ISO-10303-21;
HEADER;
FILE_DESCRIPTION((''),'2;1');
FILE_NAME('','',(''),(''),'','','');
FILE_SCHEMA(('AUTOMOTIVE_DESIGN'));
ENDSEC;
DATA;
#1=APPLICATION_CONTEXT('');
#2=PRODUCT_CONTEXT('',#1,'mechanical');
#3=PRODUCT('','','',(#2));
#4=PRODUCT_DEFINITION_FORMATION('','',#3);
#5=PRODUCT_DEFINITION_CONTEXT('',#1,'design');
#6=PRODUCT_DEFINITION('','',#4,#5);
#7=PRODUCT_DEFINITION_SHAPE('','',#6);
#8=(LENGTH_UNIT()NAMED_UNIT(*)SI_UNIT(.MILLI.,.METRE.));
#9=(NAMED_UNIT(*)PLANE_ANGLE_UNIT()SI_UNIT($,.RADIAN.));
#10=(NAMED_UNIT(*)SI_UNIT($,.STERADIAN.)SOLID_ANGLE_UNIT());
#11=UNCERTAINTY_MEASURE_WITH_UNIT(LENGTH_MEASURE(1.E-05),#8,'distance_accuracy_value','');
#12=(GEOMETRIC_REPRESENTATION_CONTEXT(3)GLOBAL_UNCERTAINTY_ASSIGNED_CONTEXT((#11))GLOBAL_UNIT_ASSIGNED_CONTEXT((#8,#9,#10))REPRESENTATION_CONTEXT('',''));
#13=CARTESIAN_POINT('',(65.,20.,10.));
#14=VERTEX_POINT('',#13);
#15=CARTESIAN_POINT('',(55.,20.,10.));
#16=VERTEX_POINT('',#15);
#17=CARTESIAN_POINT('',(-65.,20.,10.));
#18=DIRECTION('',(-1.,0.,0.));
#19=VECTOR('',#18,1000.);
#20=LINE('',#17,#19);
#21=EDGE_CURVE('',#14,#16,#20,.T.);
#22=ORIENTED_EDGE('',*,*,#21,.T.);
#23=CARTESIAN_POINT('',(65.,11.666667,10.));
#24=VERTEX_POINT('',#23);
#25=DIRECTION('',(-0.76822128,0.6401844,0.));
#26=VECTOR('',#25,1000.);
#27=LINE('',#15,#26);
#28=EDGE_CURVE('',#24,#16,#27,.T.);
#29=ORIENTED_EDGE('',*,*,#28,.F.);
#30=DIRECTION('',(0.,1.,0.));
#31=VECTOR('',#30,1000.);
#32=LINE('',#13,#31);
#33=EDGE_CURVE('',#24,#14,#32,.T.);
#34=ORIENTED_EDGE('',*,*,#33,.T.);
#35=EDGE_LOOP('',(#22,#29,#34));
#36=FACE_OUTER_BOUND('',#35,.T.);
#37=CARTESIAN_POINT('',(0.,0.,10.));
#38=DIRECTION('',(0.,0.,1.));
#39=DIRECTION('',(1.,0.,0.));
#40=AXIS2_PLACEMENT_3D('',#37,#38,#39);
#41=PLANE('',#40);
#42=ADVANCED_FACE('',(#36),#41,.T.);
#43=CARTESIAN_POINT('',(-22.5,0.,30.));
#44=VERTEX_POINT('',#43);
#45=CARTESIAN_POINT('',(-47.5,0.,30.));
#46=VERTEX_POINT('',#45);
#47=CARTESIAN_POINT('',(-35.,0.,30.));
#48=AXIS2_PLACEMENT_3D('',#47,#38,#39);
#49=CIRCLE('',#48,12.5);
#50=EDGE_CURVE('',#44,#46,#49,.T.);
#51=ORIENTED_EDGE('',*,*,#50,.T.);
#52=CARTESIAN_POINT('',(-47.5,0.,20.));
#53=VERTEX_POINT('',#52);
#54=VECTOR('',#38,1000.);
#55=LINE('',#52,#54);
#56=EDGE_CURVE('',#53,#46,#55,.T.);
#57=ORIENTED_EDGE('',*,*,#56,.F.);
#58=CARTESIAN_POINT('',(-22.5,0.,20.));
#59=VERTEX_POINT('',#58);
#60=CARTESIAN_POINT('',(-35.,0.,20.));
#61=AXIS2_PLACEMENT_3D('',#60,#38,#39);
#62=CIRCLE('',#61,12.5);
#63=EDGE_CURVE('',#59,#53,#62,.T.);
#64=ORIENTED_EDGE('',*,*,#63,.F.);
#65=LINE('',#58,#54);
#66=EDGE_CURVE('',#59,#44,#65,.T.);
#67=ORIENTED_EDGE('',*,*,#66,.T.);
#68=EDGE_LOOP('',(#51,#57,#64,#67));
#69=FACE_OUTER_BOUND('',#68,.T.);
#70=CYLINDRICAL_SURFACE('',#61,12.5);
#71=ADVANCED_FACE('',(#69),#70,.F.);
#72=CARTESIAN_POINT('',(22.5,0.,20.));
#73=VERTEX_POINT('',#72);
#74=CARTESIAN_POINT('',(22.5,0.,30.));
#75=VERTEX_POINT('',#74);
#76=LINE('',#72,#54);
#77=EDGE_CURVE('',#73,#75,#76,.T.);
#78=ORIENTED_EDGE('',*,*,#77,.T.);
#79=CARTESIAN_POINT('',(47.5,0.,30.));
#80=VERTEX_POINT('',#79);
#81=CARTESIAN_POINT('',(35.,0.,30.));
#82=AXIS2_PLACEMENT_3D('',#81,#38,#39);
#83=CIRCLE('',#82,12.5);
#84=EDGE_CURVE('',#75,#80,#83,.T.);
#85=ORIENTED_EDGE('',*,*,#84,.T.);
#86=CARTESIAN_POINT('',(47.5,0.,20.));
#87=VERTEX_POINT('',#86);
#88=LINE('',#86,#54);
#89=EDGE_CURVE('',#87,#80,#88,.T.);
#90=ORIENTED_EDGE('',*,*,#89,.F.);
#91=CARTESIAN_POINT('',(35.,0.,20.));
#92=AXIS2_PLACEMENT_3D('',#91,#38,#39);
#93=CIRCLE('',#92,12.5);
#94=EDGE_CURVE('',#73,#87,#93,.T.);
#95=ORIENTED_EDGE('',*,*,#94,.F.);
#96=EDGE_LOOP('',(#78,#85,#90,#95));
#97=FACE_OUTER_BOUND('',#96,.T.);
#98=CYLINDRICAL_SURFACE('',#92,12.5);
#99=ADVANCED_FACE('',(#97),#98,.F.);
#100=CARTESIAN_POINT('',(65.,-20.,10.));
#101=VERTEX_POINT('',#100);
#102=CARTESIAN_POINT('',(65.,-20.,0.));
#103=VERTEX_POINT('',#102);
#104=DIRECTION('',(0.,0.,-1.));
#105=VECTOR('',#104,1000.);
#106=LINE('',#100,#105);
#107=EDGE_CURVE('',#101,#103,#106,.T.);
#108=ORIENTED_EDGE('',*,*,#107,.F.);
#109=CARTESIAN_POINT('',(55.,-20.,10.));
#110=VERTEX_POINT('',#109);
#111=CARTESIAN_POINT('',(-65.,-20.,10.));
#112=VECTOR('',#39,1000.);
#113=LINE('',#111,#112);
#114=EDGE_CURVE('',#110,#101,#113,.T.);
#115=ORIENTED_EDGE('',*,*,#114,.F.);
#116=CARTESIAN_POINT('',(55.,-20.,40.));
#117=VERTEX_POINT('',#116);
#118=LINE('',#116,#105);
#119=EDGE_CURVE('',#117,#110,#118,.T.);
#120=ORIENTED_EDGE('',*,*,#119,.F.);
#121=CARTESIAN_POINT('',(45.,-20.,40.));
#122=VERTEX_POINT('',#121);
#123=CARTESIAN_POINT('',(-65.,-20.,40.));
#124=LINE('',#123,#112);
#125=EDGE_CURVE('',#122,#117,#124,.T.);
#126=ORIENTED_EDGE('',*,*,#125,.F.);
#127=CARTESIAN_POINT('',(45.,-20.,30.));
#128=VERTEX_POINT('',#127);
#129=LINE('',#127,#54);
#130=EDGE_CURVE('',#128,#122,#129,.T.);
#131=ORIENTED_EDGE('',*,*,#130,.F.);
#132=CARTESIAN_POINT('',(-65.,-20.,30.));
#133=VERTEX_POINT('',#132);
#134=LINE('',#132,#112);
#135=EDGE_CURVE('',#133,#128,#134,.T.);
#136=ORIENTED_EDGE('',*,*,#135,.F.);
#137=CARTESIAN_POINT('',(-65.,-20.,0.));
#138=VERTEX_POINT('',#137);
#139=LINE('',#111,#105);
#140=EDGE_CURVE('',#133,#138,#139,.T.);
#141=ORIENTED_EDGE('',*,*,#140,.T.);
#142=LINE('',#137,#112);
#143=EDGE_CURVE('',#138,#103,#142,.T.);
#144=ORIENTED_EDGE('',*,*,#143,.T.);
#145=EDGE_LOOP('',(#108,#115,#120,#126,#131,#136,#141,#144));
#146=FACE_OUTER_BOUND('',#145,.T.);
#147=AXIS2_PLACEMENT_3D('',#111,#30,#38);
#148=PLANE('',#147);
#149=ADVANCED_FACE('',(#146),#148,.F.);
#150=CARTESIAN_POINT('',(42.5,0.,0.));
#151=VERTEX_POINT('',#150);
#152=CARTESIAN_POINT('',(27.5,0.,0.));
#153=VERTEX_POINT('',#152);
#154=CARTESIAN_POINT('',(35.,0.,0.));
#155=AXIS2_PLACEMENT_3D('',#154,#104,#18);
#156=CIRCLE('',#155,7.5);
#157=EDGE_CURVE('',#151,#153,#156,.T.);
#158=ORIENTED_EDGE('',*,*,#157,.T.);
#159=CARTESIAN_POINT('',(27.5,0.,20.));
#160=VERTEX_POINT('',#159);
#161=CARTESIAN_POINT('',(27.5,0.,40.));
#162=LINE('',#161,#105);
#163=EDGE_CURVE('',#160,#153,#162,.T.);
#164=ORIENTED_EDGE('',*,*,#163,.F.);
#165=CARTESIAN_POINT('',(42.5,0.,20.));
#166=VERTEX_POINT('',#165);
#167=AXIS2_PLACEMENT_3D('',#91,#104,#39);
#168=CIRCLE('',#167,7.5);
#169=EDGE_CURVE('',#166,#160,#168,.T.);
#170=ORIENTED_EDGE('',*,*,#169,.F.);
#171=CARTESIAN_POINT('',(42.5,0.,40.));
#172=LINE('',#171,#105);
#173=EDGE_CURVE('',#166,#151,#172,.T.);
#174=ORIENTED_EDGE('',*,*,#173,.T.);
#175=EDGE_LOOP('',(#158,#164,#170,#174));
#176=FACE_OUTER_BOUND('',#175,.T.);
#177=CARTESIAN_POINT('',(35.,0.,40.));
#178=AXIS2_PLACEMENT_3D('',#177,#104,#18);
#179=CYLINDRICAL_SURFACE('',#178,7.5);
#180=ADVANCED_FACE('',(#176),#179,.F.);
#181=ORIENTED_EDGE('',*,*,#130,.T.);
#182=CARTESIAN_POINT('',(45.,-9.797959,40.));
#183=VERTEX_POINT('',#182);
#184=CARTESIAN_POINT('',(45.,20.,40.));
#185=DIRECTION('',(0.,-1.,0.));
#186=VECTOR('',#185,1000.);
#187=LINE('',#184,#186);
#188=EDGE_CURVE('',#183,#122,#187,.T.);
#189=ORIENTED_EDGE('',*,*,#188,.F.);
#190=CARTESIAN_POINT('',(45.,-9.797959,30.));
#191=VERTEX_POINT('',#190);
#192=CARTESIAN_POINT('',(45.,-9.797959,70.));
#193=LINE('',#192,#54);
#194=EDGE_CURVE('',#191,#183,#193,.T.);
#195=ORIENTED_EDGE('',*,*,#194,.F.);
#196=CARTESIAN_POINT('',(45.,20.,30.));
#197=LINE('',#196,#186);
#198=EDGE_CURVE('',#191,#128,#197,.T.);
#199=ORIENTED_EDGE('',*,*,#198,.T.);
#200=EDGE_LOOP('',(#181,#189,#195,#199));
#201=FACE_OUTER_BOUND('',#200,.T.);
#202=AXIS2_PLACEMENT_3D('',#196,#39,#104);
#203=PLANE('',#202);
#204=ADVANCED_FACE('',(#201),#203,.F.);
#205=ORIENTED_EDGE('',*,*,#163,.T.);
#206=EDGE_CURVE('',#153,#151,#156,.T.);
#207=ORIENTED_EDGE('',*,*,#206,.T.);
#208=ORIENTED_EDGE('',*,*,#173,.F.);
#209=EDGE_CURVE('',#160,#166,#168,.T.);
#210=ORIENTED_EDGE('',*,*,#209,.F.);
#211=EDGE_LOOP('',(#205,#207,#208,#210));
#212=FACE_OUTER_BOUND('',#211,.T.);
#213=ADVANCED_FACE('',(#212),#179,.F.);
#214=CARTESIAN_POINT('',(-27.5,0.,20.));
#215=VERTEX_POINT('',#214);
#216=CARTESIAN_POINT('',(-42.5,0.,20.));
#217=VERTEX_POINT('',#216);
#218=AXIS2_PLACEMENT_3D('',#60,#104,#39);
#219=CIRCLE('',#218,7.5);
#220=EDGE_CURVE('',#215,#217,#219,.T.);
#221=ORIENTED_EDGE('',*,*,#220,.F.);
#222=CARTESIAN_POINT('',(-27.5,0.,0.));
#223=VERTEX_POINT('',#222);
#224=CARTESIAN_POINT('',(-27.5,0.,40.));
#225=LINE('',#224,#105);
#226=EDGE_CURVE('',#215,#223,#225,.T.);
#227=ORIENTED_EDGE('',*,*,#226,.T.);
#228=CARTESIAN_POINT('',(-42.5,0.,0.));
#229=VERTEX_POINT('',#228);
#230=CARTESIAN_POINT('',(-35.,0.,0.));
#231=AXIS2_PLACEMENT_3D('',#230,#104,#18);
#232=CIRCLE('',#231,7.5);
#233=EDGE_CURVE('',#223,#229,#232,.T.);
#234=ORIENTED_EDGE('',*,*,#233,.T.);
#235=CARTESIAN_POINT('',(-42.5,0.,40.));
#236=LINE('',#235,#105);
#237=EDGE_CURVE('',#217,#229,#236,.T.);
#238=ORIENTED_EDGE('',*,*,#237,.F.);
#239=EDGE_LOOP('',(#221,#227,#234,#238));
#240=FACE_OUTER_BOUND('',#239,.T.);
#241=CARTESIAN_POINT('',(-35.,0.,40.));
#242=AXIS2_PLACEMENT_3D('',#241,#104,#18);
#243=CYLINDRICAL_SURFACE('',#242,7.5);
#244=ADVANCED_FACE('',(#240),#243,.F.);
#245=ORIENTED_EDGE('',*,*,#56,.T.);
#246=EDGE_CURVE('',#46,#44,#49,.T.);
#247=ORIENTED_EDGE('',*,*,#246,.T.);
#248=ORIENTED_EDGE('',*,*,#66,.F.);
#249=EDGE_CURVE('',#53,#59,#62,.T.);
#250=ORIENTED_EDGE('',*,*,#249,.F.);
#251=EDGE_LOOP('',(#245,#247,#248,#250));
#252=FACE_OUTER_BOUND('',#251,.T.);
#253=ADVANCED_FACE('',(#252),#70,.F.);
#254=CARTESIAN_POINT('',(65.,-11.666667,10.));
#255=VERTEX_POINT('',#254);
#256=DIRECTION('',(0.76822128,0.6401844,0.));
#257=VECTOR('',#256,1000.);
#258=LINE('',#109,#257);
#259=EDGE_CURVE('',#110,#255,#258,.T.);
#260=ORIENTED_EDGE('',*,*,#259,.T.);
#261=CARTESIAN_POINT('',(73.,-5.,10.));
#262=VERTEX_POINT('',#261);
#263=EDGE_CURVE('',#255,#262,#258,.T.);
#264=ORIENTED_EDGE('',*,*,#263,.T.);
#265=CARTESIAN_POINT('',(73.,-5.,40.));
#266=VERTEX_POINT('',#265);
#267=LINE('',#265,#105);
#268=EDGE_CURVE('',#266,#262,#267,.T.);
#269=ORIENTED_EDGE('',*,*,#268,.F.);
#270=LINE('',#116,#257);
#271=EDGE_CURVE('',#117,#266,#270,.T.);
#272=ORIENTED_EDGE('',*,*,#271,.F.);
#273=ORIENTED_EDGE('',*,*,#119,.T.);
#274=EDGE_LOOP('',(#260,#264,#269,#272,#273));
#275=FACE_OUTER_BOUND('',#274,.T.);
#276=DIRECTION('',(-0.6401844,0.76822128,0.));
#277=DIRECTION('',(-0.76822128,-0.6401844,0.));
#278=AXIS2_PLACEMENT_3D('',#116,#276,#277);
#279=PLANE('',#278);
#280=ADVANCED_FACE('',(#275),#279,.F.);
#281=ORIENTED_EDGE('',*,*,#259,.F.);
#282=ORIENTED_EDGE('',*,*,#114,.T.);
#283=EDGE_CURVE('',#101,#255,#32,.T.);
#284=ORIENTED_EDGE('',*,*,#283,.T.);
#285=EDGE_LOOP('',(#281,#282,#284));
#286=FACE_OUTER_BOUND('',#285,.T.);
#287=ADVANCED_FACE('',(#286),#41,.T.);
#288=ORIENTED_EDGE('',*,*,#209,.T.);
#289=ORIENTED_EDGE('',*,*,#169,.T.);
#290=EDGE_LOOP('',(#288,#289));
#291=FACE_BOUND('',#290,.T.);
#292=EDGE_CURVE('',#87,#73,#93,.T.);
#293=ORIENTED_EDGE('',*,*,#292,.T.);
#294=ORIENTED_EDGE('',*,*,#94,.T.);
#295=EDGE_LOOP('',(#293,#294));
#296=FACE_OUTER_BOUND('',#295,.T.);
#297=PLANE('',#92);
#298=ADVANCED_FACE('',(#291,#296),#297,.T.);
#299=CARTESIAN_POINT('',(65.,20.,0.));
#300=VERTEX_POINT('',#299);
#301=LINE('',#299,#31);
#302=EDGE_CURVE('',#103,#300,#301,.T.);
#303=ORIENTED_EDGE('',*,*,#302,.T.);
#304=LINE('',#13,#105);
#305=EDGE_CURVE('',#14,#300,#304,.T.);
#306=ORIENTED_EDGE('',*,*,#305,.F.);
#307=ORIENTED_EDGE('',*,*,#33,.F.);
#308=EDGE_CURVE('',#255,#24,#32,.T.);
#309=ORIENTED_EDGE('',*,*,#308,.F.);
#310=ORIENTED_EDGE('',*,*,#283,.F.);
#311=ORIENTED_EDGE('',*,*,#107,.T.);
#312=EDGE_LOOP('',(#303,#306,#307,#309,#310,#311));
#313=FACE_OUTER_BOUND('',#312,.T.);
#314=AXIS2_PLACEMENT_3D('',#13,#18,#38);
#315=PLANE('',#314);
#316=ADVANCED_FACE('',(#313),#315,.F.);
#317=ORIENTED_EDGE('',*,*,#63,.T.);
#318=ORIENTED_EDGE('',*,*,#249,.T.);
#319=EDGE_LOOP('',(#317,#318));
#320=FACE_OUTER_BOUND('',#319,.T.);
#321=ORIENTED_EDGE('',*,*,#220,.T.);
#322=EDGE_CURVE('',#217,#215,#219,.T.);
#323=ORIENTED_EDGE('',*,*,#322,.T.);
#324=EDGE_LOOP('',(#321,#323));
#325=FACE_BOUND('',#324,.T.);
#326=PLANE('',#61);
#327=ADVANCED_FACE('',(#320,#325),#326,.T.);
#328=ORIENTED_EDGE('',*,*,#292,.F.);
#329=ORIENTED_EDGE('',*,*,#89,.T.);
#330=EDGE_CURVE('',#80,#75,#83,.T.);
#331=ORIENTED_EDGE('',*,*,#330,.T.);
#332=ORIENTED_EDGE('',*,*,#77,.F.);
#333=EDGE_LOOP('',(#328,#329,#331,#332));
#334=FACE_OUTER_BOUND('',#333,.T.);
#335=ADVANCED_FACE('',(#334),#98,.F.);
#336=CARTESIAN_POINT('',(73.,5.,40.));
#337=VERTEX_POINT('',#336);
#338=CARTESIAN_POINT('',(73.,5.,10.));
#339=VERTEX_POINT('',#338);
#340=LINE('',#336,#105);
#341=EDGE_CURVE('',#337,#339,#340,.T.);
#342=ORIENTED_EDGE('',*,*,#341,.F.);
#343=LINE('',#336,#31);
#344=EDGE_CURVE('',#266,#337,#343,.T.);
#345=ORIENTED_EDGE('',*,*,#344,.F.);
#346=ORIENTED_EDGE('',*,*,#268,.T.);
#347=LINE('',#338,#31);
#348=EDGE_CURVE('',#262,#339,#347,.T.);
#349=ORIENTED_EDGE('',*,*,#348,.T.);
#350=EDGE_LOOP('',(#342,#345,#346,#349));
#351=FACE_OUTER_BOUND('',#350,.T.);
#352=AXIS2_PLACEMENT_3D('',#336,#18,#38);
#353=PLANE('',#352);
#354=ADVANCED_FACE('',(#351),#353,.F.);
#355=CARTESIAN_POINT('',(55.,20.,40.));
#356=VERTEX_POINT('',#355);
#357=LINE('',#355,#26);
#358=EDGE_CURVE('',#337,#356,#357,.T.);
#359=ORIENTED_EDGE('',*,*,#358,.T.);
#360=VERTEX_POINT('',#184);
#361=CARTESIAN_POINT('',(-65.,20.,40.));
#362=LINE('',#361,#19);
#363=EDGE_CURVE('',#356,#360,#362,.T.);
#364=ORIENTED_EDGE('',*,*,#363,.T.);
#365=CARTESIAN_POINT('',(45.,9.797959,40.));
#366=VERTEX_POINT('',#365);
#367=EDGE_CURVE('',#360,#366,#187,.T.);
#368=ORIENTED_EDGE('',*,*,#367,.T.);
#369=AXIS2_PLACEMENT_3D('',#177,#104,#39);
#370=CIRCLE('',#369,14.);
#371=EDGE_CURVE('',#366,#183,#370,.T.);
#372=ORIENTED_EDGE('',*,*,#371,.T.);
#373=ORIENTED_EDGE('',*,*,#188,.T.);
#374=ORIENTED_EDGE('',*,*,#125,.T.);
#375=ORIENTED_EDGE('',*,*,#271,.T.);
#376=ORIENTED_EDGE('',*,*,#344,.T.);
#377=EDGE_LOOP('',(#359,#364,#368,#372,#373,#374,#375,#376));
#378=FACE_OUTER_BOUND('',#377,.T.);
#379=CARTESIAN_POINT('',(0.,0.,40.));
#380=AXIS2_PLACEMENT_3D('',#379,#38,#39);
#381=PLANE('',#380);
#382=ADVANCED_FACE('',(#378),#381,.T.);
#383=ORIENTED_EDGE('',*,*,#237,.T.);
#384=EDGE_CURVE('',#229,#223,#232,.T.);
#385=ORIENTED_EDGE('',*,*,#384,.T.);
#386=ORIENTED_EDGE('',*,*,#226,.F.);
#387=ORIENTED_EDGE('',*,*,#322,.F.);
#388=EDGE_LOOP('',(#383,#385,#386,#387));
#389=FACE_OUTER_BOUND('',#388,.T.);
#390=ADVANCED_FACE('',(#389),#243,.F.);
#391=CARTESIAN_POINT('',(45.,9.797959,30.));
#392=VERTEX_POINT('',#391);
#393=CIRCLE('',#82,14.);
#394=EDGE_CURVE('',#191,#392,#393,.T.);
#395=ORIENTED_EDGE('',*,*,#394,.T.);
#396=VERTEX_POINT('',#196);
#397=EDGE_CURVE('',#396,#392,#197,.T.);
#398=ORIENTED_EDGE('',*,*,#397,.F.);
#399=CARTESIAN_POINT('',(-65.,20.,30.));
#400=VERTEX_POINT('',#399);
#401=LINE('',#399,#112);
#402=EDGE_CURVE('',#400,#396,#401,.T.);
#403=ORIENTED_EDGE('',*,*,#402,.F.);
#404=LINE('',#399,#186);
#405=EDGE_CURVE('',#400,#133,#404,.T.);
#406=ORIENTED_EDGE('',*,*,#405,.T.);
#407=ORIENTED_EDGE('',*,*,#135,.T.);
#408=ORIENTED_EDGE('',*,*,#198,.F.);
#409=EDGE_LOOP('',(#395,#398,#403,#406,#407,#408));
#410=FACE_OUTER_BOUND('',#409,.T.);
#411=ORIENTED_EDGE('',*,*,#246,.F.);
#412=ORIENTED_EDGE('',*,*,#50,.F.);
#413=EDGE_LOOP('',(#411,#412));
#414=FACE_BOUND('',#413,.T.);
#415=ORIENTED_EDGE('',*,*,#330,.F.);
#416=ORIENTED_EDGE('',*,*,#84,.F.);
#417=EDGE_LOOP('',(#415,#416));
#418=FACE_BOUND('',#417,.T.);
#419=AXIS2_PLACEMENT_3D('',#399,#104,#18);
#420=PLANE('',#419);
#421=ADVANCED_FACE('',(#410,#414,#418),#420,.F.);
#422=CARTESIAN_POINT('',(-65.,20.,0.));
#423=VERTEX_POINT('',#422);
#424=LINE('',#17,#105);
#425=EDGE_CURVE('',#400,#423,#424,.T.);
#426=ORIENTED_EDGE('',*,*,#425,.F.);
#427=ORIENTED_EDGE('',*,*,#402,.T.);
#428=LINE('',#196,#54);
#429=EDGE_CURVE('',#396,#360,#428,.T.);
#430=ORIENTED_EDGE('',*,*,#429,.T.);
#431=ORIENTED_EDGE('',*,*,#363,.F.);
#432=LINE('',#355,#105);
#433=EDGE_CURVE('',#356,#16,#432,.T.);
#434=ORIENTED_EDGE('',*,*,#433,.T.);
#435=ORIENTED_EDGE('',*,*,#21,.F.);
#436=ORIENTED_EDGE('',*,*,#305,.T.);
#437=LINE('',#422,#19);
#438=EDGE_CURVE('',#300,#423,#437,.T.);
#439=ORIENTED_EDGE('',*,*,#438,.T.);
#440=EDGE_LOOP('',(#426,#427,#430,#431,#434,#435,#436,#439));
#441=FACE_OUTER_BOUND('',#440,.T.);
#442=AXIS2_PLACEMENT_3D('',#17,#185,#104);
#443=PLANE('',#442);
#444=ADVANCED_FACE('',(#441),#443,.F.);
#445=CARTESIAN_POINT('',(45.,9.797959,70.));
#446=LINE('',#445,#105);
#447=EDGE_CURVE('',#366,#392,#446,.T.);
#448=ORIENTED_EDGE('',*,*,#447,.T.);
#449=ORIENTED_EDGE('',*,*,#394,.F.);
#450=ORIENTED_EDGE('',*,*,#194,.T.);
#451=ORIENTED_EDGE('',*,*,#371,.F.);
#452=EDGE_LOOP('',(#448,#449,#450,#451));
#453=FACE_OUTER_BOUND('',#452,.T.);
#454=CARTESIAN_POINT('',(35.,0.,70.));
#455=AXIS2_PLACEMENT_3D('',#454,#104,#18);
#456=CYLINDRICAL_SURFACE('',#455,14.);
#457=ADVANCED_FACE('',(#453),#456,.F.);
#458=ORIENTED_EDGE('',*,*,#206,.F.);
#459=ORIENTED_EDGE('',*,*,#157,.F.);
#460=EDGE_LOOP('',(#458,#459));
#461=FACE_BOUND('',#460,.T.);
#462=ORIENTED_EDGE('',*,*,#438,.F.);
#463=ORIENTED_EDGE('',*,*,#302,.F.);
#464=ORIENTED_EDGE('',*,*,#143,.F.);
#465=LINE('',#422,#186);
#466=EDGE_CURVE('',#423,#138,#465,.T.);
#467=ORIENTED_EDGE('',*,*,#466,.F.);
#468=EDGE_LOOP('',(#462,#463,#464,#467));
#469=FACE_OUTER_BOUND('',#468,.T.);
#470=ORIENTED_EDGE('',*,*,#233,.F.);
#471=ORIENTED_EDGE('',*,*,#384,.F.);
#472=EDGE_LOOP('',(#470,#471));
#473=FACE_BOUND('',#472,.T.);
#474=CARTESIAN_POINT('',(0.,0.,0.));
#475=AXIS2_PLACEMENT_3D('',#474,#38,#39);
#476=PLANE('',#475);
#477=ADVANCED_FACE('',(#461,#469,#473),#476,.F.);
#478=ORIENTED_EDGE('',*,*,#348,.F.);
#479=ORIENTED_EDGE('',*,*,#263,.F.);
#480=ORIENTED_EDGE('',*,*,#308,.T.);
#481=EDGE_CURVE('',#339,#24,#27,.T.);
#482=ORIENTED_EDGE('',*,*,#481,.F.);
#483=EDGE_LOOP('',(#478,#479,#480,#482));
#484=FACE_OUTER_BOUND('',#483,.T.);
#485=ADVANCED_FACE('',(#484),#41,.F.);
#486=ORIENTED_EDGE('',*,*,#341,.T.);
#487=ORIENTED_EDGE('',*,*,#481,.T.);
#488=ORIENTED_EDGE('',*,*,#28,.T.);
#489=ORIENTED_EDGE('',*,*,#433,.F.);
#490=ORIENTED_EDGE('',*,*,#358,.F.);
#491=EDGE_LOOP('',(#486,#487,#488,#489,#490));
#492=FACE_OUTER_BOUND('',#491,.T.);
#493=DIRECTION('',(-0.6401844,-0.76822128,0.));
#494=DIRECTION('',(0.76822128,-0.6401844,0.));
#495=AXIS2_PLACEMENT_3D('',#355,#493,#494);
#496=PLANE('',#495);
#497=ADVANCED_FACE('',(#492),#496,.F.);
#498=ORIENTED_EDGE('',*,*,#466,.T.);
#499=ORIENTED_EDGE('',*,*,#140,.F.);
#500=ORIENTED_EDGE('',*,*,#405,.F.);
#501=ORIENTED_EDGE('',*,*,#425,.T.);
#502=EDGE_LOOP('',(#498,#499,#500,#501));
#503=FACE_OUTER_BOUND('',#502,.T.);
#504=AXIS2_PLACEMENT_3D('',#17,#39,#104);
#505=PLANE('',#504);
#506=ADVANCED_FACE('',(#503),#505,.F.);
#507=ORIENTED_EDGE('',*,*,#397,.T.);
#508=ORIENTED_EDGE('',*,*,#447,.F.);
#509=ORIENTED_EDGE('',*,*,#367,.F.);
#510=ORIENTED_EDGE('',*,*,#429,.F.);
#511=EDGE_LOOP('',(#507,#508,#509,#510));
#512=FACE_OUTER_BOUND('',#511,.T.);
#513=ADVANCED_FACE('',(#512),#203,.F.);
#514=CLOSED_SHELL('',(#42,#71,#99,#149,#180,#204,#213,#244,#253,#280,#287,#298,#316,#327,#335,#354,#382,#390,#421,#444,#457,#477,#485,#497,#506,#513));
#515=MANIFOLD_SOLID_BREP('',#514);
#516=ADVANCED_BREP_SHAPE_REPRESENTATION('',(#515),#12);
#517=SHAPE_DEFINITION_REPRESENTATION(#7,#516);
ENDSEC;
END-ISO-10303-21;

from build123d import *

# Parameters (mm, degrees)
SKETCH1_W           = 130
SKETCH1_H           = 40
BOSS_EXTRUDE1_DEPTH = 10
BOSS_EXTRUDE2_DEPTH = 30
SKETCH3_W           = 110
SKETCH3_H           = 10
CUT_EXTRUDE1_DEPTH  = 40
SKETCH4_R           = 7.5
CUT_EXTRUDE2_DEPTH  = 40
SKETCH5_R           = 14
CUT_EXTRUDE3_DEPTH  = 40
SKETCH6_R           = 12.5
CUT_EXTRUDE4_DEPTH  = 10


with BuildPart() as part:
    # Sketch1 → Boss-Extrude1 (new body)
    with BuildSketch(Plane.XY):
        Rectangle(SKETCH1_W, SKETCH1_H)
    extrude(amount=BOSS_EXTRUDE1_DEPTH)

    # Sketch2 → Boss-Extrude2 (add)
    with BuildSketch(Plane.XY.offset(10)):
        Polygon((-65, 20), (55, 20), (73, 5), (73, -5), (55, -20), (-65, -20), align=None)
    extrude(amount=BOSS_EXTRUDE2_DEPTH)

    # Sketch3 → Cut-Extrude1 (cut)
    with BuildSketch(Plane.XZ.offset(20)):
        with Locations((-10, 35)):
            Rectangle(SKETCH3_W, SKETCH3_H)
    extrude(amount=-CUT_EXTRUDE1_DEPTH, mode=Mode.SUBTRACT)

    # Sketch4 → Cut-Extrude2 (cut)
    with BuildSketch(Plane(origin=(0, 0, 0), x_dir=(-1, 0, 0), z_dir=(0, 0, -1))):
        with Locations((-35, 0)):
            Circle(SKETCH4_R)
        with Locations((35, 0)):
            Circle(SKETCH4_R)
    extrude(amount=-CUT_EXTRUDE2_DEPTH, mode=Mode.SUBTRACT)

    # Sketch5 → Cut-Extrude3 (cut)
    with BuildSketch(Plane.XY.offset(30)):
        with Locations((-35, 0)):
            Circle(SKETCH5_R)
        with Locations((35, 0)):
            Circle(SKETCH5_R)
    extrude(amount=CUT_EXTRUDE3_DEPTH, mode=Mode.SUBTRACT)

    # Sketch6 → Cut-Extrude4 (cut)
    with BuildSketch(Plane.XY.offset(30)):
        with Locations((35, 0)):
            Circle(SKETCH6_R)
        with Locations((-35, 0)):
            Circle(SKETCH6_R)
    extrude(amount=-CUT_EXTRUDE4_DEPTH, mode=Mode.SUBTRACT)


solid = part.part
